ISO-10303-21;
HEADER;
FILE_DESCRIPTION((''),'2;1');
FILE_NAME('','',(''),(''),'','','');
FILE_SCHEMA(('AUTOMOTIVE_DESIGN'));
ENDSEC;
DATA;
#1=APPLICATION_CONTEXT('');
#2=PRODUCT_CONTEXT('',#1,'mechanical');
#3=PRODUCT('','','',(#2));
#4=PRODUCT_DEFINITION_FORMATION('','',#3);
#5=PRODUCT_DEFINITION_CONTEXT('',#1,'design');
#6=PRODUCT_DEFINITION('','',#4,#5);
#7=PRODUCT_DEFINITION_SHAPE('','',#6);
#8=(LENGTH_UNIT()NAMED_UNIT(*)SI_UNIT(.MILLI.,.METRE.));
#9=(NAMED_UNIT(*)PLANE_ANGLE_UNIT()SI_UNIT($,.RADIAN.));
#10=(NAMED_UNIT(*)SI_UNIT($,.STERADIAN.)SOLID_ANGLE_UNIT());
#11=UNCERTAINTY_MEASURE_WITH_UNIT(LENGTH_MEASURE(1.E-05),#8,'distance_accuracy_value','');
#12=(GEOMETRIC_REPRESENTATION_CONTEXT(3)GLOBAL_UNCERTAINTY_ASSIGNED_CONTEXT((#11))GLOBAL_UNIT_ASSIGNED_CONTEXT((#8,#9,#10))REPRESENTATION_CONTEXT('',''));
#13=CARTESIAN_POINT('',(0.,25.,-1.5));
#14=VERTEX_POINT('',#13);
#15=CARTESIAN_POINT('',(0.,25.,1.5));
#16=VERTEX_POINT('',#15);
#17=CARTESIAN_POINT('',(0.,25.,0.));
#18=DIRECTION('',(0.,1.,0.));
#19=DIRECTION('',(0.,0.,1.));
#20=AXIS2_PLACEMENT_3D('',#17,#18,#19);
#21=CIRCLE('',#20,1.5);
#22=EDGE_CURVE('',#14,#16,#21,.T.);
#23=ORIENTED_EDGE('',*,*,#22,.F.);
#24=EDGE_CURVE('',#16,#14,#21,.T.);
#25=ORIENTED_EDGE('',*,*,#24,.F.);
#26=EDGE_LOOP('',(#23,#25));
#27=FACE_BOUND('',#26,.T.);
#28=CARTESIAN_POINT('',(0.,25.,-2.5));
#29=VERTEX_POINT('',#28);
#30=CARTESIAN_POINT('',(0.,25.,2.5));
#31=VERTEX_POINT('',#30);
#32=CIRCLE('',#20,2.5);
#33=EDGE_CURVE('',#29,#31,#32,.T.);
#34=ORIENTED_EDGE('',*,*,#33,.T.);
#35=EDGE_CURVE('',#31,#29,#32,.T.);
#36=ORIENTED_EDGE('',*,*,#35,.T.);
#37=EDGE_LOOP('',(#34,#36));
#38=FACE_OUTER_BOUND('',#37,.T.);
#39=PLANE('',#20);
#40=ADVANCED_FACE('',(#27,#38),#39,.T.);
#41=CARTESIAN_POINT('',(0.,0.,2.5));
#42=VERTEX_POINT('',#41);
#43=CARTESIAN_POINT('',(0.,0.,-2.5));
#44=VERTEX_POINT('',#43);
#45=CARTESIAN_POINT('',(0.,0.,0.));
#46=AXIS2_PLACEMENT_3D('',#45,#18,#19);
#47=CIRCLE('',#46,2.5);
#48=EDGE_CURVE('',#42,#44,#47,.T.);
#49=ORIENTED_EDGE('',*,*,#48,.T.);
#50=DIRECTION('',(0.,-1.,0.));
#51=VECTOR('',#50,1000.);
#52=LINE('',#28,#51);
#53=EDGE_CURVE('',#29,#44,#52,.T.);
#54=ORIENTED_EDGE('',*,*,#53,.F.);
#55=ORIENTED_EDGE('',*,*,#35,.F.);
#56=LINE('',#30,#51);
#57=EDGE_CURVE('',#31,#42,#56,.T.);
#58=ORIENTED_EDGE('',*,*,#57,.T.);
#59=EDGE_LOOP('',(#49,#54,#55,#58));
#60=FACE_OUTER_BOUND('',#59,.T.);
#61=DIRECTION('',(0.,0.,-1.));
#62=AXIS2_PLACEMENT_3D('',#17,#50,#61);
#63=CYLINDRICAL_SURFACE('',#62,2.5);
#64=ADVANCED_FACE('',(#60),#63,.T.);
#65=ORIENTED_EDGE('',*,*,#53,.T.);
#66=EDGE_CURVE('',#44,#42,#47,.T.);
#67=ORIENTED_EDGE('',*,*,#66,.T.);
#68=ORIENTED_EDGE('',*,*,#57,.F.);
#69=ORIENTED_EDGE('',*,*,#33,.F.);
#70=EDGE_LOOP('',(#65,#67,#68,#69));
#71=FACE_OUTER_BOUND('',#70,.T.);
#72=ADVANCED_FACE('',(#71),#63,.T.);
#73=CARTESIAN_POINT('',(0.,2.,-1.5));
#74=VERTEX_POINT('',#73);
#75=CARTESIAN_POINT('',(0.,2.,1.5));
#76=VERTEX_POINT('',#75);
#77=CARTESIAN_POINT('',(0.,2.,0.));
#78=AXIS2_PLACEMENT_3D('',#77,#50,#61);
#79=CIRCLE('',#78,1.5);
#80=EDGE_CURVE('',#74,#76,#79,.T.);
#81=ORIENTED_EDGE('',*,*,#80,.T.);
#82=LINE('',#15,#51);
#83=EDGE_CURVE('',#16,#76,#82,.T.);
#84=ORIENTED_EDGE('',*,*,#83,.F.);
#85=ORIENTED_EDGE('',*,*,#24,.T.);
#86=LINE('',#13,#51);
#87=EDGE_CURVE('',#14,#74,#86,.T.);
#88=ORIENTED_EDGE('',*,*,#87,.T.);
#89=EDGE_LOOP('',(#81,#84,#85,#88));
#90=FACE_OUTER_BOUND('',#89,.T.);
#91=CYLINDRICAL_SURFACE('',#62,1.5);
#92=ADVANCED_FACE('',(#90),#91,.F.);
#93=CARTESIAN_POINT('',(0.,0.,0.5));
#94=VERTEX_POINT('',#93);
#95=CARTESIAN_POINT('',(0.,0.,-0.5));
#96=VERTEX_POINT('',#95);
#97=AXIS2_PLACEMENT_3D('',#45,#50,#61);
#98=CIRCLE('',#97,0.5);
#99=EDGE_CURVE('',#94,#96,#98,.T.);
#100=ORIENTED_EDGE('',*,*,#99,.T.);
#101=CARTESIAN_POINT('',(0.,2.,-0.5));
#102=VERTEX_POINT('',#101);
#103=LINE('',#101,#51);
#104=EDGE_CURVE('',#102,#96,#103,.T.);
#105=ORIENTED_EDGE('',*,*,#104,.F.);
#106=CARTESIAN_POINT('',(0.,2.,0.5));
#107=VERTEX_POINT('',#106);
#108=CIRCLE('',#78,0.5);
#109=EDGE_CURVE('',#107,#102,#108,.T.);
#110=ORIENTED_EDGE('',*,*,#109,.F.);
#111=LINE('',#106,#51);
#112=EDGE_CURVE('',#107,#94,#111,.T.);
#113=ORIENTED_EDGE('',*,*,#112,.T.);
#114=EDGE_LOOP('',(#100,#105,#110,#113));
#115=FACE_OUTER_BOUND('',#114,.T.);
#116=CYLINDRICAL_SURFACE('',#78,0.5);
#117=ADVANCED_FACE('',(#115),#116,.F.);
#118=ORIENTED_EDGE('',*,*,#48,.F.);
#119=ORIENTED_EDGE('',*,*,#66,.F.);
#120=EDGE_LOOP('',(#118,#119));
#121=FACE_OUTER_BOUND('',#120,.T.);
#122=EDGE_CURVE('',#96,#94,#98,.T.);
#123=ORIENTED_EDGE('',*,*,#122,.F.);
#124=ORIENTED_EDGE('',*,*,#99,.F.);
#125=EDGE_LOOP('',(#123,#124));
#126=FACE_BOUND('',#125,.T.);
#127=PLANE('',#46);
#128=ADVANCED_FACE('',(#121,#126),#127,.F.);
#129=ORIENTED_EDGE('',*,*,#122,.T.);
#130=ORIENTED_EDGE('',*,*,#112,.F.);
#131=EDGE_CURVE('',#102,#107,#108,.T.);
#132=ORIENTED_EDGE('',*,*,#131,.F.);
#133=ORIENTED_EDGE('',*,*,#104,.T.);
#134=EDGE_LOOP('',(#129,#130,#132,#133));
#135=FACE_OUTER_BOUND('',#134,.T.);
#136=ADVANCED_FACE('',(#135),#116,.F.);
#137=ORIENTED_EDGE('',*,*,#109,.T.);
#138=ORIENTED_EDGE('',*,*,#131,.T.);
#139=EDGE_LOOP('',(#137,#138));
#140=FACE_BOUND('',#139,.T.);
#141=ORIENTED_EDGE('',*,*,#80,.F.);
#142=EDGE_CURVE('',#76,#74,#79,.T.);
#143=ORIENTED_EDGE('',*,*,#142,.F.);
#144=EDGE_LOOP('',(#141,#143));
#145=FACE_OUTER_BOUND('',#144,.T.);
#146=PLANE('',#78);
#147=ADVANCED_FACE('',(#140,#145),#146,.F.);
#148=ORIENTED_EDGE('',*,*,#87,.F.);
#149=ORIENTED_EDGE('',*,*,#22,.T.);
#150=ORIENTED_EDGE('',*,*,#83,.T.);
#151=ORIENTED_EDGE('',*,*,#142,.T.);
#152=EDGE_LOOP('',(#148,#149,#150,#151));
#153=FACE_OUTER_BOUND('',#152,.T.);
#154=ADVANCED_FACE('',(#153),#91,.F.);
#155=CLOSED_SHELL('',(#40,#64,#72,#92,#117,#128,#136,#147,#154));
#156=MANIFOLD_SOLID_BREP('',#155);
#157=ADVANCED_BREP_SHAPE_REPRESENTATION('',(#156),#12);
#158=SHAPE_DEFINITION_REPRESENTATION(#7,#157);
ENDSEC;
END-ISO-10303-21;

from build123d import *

# Parameters (mm, degrees)
SKETCH1_R           = 2.5
SKETCH1_R_2         = 1.5
BOSS_EXTRUDE1_DEPTH = 25
SKETCH2_R           = 1.5
SKETCH2_R_2         = 0.5
BOSS_EXTRUDE2_DEPTH = 2


with BuildPart() as part:
    # Sketch1 → Boss-Extrude1 (new body)
    with BuildSketch(Plane(origin=(0, 0, 0), x_dir=(1, 0, 0), z_dir=(0, 1, 0))):
        with Locations(Location((0, 0, 0), (0, 0, 270))):
            Circle(SKETCH1_R)
        with Locations(Location((0, 0, 0), (0, 0, 270))):
            Circle(SKETCH1_R_2, mode=Mode.SUBTRACT)
    extrude(amount=BOSS_EXTRUDE1_DEPTH)

    # Sketch2 → Boss-Extrude2 (add)
    with BuildSketch(Plane.XZ):
        with Locations(Location((0, 0, 0), (0, 0, 270))):
            Circle(SKETCH2_R)
        with Locations(Location((0, 0, 0), (0, 0, 270))):
            Circle(SKETCH2_R_2, mode=Mode.SUBTRACT)
    extrude(amount=-BOSS_EXTRUDE2_DEPTH)


solid = part.part
